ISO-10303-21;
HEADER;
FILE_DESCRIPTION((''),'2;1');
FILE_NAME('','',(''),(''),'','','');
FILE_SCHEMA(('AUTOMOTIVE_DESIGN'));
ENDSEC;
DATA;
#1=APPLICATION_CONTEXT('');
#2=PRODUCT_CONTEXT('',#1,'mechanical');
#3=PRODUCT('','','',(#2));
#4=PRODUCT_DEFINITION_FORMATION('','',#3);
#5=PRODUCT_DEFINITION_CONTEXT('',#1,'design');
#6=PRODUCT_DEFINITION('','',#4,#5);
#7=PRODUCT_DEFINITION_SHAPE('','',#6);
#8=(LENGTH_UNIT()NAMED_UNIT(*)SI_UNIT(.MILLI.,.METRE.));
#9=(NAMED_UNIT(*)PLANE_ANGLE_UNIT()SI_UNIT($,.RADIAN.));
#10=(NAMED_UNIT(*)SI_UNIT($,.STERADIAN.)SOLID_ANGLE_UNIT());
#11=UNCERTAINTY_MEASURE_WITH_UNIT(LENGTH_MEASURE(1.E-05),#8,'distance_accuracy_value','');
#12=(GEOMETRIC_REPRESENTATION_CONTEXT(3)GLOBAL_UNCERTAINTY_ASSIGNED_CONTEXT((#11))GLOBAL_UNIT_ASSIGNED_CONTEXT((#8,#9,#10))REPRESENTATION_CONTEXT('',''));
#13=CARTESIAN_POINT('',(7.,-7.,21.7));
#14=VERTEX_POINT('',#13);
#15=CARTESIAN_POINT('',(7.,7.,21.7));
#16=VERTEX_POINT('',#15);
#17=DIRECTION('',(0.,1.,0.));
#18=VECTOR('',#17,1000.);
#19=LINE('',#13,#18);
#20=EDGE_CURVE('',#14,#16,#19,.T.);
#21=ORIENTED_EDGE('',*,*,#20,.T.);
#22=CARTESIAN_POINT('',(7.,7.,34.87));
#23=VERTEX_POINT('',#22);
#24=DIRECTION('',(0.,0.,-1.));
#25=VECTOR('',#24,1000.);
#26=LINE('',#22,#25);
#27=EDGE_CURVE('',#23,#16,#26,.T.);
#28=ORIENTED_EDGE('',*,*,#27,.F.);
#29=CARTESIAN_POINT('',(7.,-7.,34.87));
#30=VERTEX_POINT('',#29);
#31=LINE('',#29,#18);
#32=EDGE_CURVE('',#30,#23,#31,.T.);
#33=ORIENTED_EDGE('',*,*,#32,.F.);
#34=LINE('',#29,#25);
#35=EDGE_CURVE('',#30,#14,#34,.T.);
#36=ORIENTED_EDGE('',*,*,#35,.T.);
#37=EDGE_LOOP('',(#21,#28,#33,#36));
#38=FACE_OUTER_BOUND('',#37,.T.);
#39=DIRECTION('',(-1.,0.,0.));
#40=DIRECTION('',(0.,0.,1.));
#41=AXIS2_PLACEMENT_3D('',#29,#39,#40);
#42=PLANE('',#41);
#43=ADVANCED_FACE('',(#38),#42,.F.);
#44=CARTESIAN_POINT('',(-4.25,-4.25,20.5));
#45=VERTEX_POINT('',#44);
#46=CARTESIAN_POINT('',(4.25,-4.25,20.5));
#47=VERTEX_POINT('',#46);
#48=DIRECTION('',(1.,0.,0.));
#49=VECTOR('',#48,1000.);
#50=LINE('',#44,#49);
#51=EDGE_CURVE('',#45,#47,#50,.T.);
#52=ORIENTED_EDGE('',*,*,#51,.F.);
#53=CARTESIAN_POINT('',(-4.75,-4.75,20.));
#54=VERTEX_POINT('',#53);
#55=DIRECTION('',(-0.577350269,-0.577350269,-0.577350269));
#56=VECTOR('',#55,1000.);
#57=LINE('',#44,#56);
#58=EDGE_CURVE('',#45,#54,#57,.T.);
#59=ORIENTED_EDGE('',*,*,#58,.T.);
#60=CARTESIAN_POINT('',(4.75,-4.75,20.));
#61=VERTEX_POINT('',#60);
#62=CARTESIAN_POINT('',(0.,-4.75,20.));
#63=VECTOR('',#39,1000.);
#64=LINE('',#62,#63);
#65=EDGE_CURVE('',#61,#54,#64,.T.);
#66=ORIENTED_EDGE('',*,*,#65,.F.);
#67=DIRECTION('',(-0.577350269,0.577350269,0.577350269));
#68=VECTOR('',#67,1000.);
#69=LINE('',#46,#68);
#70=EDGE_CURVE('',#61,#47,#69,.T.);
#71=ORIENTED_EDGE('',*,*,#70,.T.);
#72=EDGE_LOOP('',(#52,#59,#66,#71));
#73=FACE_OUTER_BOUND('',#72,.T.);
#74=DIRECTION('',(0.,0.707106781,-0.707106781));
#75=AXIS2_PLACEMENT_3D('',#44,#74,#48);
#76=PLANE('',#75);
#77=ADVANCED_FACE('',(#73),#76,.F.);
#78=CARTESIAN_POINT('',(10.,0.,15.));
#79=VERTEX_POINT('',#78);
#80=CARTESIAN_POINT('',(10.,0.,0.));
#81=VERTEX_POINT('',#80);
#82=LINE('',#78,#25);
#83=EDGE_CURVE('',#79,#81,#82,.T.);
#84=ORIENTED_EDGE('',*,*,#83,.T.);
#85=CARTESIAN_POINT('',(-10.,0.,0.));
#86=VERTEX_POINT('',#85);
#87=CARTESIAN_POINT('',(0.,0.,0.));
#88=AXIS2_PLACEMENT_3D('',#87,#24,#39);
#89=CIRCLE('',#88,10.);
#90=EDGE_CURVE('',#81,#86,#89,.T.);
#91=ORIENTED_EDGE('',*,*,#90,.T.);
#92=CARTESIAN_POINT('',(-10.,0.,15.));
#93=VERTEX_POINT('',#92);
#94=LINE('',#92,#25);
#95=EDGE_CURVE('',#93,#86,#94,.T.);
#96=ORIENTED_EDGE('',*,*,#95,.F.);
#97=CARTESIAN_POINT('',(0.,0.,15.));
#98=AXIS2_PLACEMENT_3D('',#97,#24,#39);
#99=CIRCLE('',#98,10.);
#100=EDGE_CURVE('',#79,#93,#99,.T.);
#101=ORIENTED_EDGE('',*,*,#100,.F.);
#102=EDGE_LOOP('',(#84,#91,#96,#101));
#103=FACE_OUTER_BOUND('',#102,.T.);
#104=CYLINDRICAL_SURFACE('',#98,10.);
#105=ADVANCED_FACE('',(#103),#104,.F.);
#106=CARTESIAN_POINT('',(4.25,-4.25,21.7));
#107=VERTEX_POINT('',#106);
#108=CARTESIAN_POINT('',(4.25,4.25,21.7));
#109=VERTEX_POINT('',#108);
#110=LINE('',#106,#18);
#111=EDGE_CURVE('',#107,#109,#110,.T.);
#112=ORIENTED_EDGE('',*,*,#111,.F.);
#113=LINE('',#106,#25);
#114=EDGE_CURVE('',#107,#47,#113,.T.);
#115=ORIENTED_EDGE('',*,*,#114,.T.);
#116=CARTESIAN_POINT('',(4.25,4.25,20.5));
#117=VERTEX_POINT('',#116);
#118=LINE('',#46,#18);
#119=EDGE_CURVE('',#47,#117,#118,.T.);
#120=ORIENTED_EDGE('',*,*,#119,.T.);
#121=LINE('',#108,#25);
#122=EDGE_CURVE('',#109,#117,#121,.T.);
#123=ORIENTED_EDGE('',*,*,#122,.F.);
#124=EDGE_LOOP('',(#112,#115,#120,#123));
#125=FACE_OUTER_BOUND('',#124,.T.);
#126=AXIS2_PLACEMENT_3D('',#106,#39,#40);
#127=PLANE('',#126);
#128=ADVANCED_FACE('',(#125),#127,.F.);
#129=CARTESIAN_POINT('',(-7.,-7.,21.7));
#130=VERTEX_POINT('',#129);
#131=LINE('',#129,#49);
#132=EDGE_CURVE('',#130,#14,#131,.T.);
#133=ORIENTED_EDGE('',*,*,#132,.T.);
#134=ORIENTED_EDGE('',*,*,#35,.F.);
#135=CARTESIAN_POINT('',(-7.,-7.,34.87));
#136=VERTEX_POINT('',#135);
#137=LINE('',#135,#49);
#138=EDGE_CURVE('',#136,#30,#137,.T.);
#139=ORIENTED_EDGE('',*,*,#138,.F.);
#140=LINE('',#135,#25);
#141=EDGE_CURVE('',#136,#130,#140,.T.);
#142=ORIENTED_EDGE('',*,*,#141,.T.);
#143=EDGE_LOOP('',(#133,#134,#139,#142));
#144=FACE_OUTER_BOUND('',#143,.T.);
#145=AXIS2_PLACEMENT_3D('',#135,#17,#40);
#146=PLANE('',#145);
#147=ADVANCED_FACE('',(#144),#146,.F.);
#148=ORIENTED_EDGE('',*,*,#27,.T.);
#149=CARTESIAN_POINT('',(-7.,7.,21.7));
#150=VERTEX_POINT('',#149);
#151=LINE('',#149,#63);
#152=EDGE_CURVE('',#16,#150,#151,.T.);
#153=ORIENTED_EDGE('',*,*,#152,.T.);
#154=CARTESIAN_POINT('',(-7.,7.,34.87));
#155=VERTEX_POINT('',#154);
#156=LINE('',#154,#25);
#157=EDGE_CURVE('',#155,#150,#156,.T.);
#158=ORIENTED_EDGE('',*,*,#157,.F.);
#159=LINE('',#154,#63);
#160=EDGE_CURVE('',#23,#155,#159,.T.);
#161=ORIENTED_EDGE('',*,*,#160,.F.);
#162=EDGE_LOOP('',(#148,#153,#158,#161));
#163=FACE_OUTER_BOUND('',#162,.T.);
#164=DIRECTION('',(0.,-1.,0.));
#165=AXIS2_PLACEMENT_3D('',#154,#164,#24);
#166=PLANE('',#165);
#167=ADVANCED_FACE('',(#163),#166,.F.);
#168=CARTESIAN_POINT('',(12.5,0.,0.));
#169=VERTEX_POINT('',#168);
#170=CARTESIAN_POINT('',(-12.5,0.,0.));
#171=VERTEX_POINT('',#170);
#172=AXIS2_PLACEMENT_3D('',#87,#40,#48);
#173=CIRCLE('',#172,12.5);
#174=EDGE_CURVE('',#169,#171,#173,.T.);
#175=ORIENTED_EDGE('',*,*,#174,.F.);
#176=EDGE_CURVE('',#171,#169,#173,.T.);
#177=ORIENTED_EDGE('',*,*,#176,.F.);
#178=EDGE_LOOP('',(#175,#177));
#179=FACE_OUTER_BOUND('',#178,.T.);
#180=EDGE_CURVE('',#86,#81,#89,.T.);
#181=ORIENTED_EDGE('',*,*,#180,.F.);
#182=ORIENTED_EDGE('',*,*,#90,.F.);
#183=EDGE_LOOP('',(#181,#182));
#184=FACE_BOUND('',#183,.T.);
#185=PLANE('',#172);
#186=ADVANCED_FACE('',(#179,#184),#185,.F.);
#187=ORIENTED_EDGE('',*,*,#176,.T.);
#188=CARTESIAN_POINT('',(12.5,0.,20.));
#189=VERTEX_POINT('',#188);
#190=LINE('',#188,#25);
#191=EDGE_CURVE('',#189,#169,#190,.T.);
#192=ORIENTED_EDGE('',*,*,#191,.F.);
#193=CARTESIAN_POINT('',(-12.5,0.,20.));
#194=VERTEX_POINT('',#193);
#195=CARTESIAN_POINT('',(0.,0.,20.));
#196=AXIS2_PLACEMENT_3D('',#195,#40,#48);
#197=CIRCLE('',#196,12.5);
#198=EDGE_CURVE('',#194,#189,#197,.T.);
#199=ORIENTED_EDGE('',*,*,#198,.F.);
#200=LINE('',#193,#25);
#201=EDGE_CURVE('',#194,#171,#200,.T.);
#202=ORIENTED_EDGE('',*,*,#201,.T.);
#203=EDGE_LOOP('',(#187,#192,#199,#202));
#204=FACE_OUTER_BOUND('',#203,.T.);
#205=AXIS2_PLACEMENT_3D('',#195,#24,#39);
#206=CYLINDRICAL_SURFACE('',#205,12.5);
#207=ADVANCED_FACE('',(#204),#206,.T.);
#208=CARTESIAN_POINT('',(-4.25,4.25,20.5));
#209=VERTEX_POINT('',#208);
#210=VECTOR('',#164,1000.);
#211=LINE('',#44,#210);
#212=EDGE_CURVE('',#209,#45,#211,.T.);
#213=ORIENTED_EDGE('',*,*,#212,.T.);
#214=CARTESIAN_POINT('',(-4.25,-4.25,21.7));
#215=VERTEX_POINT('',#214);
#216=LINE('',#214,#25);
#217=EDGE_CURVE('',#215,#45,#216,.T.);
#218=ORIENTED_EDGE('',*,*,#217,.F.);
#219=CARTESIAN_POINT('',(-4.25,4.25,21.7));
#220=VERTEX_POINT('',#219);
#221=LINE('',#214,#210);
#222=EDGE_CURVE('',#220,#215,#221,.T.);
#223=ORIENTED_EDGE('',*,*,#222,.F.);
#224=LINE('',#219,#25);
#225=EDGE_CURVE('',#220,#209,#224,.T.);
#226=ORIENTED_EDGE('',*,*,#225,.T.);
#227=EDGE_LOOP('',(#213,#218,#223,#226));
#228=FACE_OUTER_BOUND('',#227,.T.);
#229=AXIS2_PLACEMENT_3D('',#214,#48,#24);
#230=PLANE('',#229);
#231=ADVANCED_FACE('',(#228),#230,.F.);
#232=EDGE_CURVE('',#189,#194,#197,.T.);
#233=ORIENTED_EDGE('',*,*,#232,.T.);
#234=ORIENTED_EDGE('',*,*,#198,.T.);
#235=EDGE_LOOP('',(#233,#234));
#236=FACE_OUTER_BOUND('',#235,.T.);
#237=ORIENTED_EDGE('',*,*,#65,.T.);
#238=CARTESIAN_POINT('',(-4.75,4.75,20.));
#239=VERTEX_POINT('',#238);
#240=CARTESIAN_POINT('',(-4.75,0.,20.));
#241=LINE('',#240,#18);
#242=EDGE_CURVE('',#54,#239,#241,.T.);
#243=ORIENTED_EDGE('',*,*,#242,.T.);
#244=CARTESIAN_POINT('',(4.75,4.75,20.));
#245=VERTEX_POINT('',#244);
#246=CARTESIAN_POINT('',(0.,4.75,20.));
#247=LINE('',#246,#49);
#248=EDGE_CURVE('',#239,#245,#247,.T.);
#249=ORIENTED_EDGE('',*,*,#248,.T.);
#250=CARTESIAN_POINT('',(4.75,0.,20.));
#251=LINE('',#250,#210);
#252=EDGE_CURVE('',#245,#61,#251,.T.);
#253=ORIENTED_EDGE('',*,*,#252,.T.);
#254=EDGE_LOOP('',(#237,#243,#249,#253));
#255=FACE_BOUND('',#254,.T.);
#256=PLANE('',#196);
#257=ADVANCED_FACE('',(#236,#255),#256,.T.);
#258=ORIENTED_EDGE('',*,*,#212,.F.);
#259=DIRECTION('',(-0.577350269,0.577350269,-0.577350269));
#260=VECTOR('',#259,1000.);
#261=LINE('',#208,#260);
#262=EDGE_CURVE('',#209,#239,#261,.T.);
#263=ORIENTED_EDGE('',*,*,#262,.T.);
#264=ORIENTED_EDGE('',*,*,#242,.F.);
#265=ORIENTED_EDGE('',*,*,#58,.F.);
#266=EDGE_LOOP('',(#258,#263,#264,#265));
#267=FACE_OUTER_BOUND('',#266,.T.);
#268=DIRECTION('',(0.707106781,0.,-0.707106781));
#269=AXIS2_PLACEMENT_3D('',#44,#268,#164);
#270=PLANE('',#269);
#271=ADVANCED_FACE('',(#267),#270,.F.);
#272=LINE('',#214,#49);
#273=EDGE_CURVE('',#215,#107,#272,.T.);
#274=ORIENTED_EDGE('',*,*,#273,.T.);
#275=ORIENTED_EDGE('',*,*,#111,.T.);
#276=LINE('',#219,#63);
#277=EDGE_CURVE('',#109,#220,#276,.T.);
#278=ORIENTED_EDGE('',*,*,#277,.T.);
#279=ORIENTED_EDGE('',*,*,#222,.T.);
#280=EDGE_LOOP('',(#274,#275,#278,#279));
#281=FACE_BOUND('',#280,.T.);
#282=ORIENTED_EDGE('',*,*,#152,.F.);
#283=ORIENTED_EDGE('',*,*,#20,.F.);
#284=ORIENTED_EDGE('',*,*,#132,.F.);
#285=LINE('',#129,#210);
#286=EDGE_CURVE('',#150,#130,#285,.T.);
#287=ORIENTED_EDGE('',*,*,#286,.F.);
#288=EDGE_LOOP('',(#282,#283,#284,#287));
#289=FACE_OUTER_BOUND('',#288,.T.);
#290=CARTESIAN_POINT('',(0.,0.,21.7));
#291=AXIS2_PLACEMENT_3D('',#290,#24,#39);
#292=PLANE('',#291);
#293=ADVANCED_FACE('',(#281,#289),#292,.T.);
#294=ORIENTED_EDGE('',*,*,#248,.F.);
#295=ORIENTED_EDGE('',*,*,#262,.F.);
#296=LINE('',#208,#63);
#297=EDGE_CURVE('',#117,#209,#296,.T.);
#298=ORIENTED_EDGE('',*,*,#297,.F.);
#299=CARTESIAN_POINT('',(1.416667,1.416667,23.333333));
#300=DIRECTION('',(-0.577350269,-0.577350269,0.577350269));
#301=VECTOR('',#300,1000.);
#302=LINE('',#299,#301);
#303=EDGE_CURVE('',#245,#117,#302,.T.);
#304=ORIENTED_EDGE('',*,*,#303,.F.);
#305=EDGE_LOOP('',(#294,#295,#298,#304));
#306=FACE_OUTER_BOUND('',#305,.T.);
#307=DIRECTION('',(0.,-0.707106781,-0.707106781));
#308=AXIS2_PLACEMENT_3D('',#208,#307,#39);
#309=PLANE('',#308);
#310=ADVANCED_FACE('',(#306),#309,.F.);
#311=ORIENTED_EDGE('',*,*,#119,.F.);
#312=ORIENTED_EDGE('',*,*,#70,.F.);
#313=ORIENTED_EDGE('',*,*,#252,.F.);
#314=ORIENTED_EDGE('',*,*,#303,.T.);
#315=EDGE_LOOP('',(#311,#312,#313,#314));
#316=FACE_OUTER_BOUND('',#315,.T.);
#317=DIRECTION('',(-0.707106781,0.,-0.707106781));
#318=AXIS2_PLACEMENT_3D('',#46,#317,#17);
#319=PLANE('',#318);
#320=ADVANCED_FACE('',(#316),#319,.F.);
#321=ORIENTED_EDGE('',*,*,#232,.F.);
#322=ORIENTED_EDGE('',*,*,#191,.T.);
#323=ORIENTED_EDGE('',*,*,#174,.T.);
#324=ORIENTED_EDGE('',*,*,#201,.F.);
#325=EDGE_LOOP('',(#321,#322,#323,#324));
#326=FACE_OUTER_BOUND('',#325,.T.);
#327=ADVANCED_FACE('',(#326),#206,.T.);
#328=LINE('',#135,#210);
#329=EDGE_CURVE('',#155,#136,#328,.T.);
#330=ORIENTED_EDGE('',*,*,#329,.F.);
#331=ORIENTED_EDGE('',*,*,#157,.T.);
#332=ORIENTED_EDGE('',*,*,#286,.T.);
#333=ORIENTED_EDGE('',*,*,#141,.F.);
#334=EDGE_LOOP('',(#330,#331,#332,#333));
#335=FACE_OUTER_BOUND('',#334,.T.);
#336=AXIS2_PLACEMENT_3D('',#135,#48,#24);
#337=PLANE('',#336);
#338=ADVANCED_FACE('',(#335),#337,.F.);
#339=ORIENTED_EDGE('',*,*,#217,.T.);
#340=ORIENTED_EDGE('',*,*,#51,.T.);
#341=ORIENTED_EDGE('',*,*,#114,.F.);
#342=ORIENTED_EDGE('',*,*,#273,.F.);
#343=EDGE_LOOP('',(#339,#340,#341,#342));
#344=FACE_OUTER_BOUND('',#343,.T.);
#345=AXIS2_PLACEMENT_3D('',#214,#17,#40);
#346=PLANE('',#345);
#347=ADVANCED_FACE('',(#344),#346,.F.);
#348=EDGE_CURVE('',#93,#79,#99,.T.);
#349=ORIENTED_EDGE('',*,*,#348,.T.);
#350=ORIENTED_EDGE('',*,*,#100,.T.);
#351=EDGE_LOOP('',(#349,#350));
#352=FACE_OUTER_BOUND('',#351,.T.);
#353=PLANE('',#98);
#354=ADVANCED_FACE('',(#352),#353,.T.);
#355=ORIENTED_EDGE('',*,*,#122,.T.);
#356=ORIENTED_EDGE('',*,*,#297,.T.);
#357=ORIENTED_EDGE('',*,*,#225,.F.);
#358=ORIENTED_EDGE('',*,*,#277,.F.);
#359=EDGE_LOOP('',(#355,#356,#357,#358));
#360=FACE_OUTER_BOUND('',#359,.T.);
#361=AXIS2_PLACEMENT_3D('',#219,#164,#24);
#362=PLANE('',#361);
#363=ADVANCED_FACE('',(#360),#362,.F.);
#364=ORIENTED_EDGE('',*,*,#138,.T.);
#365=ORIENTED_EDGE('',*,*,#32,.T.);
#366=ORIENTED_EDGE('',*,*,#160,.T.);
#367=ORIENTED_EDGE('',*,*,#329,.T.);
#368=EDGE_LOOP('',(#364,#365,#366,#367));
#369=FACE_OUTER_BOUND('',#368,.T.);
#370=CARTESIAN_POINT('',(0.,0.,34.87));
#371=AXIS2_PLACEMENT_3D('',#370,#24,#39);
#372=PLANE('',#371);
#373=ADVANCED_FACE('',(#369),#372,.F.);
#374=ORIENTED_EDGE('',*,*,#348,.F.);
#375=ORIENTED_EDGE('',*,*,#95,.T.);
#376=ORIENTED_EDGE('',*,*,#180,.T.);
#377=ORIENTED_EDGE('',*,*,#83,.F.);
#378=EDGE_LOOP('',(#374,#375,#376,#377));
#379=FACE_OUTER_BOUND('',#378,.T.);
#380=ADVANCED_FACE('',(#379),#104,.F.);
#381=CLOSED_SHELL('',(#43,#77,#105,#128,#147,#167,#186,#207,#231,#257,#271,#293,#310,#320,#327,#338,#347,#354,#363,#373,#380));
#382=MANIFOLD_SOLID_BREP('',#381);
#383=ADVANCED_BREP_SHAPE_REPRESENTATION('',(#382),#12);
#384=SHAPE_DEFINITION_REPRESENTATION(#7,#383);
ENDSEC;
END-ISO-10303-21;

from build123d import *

# Parameters (mm, degrees)
SKETCH_1_R          = 12.5
EXTRUDE_1_DEPTH     = 20
SKETCH_2_W          = 8.5
SKETCH_2_H          = 8.5
EXTRUDE_2_DEPTH     = 1.7
SKETCH_3_W          = 14
SKETCH_3_H          = 14
EXTRUDE_3_DEPTH     = 13.17
SKETCH_4_R          = 10
CUT_EXTRUDE_1_DEPTH = 15
CHAMFER_1_SIZE      = 0.5


with BuildPart() as part:
    # 草图1 → 凸台-拉伸1 (new body)
    with BuildSketch(Plane.XY):
        Circle(SKETCH_1_R)
    extrude(amount=EXTRUDE_1_DEPTH)

    # 草图2 → 凸台-拉伸2 (add)
    with BuildSketch(Plane.XY.offset(20)):
        Rectangle(SKETCH_2_W, SKETCH_2_H)
    extrude(amount=EXTRUDE_2_DEPTH)

    # 草图3 → 凸台-拉伸3 (add)
    with BuildSketch(Plane.XY.offset(21.7)):
        Rectangle(SKETCH_3_W, SKETCH_3_H)
    extrude(amount=EXTRUDE_3_DEPTH)

    # 草图4 → 切除-拉伸1 (cut)
    with BuildSketch(Plane(origin=(0, 0, 0), x_dir=(-1, 0, 0), z_dir=(0, 0, -1))):
        Circle(SKETCH_4_R)
    extrude(amount=-CUT_EXTRUDE_1_DEPTH, mode=Mode.SUBTRACT)

    # 倒角1
    chamfer_1_edges = [part.edges().sort_by_distance(p)[0] for p in [
        (4.25, 0, 20),
        (0, 4.25, 20),
        (-4.25, 0, 20),
        (0, -4.25, 20),
    ]]
    chamfer(chamfer_1_edges, length=CHAMFER_1_SIZE)


solid = part.part
